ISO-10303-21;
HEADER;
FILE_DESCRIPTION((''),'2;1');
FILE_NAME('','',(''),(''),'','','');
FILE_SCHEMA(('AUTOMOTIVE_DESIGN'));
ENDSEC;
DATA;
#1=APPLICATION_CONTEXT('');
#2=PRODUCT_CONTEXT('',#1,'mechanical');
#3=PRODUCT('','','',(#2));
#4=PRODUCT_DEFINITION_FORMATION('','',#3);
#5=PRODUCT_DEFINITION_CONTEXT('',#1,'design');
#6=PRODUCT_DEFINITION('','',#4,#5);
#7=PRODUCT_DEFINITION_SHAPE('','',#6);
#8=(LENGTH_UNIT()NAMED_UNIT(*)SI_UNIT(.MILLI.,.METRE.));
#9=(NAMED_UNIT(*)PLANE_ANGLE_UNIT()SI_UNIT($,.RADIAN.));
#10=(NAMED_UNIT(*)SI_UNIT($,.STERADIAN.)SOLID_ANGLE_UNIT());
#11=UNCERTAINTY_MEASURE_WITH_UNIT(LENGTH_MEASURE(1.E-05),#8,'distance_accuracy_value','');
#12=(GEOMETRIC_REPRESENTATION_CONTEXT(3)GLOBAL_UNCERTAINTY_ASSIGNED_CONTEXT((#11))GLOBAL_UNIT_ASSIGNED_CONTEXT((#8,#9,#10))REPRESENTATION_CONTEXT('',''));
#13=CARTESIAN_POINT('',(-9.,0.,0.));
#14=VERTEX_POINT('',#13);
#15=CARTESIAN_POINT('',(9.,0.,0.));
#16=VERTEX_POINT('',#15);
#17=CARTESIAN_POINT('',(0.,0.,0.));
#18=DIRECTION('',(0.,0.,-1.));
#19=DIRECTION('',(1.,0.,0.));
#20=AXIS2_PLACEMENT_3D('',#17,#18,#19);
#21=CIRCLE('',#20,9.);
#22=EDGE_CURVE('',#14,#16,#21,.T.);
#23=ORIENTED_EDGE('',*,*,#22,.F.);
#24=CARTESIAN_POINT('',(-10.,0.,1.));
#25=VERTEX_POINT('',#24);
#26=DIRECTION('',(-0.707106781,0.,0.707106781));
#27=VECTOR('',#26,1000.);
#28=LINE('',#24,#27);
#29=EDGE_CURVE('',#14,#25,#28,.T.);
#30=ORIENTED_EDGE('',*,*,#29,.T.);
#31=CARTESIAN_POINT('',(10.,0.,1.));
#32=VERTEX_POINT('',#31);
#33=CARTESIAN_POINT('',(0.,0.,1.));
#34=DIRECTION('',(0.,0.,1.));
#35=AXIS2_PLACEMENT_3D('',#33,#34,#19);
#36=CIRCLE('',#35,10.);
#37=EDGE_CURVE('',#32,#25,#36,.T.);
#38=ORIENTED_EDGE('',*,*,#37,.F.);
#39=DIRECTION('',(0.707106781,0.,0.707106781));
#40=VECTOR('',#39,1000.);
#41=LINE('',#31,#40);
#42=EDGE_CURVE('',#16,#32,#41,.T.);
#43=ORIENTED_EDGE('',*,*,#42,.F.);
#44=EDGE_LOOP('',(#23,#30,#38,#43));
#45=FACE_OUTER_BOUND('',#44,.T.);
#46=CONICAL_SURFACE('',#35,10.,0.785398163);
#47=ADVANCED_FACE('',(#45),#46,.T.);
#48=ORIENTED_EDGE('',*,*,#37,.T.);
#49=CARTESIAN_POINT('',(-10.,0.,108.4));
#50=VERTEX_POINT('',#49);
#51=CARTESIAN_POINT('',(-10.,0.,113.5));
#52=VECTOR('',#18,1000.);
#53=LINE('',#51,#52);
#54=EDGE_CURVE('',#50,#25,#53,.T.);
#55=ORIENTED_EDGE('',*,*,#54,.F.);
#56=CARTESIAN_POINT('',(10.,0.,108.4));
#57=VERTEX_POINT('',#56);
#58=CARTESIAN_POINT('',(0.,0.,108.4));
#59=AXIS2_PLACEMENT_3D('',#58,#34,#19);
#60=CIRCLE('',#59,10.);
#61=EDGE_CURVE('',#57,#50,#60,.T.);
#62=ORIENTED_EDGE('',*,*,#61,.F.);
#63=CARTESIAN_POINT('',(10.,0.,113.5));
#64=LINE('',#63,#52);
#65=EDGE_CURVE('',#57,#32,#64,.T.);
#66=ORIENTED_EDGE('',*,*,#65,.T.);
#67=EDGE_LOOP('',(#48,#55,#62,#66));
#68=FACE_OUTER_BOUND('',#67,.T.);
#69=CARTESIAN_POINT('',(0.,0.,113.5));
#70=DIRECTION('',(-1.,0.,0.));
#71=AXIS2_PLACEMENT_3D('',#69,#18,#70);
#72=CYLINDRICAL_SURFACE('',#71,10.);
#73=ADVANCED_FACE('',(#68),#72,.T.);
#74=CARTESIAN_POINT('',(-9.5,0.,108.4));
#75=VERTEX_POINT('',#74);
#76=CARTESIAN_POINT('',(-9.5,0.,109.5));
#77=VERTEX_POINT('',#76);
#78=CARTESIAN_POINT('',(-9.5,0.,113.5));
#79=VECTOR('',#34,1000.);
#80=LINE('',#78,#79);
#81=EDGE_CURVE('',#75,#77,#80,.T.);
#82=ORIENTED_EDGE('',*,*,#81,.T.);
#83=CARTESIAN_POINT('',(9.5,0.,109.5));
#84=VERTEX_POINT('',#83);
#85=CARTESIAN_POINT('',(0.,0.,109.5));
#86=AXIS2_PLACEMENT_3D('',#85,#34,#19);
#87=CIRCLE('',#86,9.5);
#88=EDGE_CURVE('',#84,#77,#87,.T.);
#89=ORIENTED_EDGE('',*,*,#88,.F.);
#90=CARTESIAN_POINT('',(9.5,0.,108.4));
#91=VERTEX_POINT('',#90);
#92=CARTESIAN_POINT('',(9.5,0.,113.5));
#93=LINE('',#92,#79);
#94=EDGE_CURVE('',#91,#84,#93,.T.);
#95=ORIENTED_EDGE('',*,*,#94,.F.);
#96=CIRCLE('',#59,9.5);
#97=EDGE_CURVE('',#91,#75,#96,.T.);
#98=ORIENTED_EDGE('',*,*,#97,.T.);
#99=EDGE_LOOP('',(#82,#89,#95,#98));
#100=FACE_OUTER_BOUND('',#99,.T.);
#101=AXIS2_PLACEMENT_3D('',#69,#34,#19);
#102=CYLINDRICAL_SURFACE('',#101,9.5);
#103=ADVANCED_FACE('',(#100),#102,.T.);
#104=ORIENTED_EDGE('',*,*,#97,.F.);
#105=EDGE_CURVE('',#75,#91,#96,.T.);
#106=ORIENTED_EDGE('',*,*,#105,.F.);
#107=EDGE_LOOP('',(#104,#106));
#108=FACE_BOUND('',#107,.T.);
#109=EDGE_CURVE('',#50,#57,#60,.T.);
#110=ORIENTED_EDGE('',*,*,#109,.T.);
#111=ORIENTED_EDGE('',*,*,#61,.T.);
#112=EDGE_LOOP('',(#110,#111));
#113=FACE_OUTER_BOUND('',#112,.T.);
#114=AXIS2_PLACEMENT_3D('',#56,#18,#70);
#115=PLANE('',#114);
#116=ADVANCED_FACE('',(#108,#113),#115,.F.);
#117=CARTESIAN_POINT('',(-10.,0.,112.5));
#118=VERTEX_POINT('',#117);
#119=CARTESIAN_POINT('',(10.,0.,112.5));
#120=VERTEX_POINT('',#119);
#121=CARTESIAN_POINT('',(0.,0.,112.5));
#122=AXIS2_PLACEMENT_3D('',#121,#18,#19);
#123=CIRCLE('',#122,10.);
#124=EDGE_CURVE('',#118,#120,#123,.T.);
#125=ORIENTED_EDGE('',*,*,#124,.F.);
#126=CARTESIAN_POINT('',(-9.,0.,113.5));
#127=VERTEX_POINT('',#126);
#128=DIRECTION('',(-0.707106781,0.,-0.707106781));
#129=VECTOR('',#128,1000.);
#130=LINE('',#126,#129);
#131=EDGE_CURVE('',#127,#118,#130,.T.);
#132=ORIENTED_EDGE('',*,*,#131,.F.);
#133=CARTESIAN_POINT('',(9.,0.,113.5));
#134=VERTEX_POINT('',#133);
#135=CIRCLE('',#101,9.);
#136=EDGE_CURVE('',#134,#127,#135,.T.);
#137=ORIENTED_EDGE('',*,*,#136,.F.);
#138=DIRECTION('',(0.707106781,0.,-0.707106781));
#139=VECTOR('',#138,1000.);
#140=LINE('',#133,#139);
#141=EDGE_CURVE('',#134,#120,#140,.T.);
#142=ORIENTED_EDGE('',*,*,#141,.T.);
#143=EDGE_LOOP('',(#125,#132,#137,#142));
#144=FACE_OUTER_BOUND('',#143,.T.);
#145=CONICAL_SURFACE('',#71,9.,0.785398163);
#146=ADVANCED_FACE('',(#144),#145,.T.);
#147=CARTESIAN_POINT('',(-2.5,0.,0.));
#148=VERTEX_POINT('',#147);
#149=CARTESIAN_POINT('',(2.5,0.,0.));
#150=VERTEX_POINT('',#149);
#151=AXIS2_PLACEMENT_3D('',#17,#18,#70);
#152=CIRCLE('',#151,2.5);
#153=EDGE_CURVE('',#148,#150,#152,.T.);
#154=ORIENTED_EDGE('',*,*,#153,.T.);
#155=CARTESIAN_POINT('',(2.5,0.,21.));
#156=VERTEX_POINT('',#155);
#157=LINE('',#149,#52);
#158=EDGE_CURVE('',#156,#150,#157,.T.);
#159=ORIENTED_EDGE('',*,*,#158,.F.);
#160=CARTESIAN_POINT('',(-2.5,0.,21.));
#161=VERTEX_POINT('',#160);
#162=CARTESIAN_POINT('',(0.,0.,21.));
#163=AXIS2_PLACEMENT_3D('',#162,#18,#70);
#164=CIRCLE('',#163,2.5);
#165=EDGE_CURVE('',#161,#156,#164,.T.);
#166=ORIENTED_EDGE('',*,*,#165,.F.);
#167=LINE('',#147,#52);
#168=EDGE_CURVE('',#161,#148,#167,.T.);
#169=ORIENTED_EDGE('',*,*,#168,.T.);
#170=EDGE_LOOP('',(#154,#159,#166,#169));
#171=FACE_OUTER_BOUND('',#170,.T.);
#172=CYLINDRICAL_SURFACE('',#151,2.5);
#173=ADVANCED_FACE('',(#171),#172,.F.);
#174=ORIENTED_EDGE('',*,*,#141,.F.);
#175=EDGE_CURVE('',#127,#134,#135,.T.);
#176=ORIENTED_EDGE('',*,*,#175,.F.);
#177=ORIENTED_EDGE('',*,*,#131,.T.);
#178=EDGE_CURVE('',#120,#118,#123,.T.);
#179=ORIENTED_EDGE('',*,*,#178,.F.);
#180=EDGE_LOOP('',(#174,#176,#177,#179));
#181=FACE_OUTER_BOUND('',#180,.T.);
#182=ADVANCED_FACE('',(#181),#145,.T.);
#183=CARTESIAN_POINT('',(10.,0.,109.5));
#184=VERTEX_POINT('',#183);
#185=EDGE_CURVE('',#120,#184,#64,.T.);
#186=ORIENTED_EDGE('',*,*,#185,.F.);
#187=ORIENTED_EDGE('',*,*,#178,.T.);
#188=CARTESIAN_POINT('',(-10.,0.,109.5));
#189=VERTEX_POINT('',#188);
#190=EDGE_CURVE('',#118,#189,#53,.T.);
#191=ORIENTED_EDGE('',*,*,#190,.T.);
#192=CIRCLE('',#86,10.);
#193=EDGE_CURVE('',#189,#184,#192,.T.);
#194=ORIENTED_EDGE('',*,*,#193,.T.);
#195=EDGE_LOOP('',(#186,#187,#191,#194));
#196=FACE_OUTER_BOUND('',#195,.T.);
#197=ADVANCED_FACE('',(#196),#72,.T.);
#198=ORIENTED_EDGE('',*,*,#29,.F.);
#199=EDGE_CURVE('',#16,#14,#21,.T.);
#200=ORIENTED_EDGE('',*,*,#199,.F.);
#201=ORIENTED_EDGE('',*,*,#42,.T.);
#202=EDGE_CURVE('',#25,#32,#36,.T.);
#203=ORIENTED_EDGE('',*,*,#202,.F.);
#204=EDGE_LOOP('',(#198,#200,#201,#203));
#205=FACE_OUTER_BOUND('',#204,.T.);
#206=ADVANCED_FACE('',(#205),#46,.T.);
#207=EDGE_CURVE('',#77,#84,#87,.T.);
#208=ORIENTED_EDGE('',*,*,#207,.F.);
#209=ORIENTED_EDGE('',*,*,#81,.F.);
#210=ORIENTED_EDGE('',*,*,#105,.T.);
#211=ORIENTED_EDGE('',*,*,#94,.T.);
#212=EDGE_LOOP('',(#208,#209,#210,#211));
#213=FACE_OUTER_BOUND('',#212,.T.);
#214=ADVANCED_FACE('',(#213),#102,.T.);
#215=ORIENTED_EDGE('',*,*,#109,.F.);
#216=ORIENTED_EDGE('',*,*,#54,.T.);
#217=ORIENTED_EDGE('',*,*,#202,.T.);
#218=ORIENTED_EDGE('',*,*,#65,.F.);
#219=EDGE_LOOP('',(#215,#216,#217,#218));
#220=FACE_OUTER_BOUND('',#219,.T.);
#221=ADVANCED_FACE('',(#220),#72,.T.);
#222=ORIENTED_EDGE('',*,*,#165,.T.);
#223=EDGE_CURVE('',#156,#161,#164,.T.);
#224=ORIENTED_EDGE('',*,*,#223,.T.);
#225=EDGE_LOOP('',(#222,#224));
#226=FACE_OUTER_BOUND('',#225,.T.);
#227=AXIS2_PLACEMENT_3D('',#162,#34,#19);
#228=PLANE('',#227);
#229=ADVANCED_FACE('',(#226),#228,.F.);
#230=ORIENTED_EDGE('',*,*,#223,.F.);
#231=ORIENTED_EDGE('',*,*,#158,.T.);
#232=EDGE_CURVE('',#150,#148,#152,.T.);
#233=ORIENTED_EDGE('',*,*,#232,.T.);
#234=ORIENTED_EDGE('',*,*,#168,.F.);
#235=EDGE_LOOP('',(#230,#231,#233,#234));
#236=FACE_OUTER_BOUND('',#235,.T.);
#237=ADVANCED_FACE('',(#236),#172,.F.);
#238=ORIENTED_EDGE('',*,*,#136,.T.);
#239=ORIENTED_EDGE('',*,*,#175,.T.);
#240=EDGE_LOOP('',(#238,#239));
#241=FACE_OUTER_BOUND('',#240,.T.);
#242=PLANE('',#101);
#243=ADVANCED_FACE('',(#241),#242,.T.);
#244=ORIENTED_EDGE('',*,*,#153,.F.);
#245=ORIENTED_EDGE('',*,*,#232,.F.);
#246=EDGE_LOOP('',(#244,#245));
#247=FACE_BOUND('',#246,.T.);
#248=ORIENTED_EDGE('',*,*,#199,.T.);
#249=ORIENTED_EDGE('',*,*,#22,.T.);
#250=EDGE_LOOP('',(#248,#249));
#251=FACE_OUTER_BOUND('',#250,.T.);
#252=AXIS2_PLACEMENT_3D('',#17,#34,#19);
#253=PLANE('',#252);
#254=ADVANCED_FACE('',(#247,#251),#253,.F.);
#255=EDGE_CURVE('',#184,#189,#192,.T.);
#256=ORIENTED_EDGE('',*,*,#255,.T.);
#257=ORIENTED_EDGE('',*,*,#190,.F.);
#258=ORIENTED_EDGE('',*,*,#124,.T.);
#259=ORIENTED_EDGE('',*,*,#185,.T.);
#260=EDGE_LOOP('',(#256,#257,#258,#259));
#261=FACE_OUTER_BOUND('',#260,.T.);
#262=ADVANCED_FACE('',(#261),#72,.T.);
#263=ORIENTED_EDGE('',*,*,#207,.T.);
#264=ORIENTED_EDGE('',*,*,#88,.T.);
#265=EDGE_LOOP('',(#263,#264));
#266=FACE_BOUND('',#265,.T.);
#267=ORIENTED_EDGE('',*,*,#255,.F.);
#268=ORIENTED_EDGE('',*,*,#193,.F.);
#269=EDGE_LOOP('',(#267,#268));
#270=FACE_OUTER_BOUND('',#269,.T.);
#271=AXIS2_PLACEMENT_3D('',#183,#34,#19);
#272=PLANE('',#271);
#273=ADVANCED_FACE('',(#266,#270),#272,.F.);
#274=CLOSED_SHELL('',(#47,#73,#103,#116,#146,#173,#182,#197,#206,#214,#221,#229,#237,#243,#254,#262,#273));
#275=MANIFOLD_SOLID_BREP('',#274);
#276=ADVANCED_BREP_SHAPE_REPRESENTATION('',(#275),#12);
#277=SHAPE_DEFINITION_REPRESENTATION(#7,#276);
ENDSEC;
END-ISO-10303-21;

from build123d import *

# Parameters (mm, degrees)
SKETCH_1_R             = 10
EXTRUDE_1_DEPTH        = 113.5
SKETCH_2_W             = 0.5
SKETCH_2_H             = 1.1
CHAMFER_1_SIZE         = 1
HOLE_WIZARD_M6_1_D     = 5
HOLE_WIZARD_M6_1_DEPTH = 21


with BuildPart() as part:
    # 草图1 → 凸台-拉伸1 (new body)
    with BuildSketch(Plane.XY):
        with Locations(Location((0, 0, 0), (0, 0, 180))):
            Circle(SKETCH_1_R)
    extrude(amount=EXTRUDE_1_DEPTH)

    # 草图2 → 切除-旋转1 (revolve, cut)
    with BuildSketch(Plane(origin=(0, 0, 0), x_dir=(1, 0, 0), z_dir=(0, 1, 0)), mode=Mode.PRIVATE) as cut_revolve_1_sk:
        with Locations((9.75, -108.95)):
            Rectangle(SKETCH_2_W, SKETCH_2_H)
    revolve(cut_revolve_1_sk.sketch.rotate(Axis((0, 0, 113.5), (0, 0, -1)), 180), axis=Axis((0, 0, 113.5), (0, 0, -1)), mode=Mode.SUBTRACT)

    # 倒角1
    chamfer_1_edges = [part.edges().sort_by_distance(p)[0] for p in [
        (10, 0, 0),
        (10, 0, 113.5),
    ]]
    chamfer(chamfer_1_edges, length=CHAMFER_1_SIZE)

    # M6 螺纹孔1
    with Locations(Plane(origin=(0, 0, 0), x_dir=(-1, 0, 0), z_dir=(0, 0, -1))):
        with Locations((0, 0)):
            Hole(HOLE_WIZARD_M6_1_D / 2, depth=HOLE_WIZARD_M6_1_DEPTH)


solid = part.part
